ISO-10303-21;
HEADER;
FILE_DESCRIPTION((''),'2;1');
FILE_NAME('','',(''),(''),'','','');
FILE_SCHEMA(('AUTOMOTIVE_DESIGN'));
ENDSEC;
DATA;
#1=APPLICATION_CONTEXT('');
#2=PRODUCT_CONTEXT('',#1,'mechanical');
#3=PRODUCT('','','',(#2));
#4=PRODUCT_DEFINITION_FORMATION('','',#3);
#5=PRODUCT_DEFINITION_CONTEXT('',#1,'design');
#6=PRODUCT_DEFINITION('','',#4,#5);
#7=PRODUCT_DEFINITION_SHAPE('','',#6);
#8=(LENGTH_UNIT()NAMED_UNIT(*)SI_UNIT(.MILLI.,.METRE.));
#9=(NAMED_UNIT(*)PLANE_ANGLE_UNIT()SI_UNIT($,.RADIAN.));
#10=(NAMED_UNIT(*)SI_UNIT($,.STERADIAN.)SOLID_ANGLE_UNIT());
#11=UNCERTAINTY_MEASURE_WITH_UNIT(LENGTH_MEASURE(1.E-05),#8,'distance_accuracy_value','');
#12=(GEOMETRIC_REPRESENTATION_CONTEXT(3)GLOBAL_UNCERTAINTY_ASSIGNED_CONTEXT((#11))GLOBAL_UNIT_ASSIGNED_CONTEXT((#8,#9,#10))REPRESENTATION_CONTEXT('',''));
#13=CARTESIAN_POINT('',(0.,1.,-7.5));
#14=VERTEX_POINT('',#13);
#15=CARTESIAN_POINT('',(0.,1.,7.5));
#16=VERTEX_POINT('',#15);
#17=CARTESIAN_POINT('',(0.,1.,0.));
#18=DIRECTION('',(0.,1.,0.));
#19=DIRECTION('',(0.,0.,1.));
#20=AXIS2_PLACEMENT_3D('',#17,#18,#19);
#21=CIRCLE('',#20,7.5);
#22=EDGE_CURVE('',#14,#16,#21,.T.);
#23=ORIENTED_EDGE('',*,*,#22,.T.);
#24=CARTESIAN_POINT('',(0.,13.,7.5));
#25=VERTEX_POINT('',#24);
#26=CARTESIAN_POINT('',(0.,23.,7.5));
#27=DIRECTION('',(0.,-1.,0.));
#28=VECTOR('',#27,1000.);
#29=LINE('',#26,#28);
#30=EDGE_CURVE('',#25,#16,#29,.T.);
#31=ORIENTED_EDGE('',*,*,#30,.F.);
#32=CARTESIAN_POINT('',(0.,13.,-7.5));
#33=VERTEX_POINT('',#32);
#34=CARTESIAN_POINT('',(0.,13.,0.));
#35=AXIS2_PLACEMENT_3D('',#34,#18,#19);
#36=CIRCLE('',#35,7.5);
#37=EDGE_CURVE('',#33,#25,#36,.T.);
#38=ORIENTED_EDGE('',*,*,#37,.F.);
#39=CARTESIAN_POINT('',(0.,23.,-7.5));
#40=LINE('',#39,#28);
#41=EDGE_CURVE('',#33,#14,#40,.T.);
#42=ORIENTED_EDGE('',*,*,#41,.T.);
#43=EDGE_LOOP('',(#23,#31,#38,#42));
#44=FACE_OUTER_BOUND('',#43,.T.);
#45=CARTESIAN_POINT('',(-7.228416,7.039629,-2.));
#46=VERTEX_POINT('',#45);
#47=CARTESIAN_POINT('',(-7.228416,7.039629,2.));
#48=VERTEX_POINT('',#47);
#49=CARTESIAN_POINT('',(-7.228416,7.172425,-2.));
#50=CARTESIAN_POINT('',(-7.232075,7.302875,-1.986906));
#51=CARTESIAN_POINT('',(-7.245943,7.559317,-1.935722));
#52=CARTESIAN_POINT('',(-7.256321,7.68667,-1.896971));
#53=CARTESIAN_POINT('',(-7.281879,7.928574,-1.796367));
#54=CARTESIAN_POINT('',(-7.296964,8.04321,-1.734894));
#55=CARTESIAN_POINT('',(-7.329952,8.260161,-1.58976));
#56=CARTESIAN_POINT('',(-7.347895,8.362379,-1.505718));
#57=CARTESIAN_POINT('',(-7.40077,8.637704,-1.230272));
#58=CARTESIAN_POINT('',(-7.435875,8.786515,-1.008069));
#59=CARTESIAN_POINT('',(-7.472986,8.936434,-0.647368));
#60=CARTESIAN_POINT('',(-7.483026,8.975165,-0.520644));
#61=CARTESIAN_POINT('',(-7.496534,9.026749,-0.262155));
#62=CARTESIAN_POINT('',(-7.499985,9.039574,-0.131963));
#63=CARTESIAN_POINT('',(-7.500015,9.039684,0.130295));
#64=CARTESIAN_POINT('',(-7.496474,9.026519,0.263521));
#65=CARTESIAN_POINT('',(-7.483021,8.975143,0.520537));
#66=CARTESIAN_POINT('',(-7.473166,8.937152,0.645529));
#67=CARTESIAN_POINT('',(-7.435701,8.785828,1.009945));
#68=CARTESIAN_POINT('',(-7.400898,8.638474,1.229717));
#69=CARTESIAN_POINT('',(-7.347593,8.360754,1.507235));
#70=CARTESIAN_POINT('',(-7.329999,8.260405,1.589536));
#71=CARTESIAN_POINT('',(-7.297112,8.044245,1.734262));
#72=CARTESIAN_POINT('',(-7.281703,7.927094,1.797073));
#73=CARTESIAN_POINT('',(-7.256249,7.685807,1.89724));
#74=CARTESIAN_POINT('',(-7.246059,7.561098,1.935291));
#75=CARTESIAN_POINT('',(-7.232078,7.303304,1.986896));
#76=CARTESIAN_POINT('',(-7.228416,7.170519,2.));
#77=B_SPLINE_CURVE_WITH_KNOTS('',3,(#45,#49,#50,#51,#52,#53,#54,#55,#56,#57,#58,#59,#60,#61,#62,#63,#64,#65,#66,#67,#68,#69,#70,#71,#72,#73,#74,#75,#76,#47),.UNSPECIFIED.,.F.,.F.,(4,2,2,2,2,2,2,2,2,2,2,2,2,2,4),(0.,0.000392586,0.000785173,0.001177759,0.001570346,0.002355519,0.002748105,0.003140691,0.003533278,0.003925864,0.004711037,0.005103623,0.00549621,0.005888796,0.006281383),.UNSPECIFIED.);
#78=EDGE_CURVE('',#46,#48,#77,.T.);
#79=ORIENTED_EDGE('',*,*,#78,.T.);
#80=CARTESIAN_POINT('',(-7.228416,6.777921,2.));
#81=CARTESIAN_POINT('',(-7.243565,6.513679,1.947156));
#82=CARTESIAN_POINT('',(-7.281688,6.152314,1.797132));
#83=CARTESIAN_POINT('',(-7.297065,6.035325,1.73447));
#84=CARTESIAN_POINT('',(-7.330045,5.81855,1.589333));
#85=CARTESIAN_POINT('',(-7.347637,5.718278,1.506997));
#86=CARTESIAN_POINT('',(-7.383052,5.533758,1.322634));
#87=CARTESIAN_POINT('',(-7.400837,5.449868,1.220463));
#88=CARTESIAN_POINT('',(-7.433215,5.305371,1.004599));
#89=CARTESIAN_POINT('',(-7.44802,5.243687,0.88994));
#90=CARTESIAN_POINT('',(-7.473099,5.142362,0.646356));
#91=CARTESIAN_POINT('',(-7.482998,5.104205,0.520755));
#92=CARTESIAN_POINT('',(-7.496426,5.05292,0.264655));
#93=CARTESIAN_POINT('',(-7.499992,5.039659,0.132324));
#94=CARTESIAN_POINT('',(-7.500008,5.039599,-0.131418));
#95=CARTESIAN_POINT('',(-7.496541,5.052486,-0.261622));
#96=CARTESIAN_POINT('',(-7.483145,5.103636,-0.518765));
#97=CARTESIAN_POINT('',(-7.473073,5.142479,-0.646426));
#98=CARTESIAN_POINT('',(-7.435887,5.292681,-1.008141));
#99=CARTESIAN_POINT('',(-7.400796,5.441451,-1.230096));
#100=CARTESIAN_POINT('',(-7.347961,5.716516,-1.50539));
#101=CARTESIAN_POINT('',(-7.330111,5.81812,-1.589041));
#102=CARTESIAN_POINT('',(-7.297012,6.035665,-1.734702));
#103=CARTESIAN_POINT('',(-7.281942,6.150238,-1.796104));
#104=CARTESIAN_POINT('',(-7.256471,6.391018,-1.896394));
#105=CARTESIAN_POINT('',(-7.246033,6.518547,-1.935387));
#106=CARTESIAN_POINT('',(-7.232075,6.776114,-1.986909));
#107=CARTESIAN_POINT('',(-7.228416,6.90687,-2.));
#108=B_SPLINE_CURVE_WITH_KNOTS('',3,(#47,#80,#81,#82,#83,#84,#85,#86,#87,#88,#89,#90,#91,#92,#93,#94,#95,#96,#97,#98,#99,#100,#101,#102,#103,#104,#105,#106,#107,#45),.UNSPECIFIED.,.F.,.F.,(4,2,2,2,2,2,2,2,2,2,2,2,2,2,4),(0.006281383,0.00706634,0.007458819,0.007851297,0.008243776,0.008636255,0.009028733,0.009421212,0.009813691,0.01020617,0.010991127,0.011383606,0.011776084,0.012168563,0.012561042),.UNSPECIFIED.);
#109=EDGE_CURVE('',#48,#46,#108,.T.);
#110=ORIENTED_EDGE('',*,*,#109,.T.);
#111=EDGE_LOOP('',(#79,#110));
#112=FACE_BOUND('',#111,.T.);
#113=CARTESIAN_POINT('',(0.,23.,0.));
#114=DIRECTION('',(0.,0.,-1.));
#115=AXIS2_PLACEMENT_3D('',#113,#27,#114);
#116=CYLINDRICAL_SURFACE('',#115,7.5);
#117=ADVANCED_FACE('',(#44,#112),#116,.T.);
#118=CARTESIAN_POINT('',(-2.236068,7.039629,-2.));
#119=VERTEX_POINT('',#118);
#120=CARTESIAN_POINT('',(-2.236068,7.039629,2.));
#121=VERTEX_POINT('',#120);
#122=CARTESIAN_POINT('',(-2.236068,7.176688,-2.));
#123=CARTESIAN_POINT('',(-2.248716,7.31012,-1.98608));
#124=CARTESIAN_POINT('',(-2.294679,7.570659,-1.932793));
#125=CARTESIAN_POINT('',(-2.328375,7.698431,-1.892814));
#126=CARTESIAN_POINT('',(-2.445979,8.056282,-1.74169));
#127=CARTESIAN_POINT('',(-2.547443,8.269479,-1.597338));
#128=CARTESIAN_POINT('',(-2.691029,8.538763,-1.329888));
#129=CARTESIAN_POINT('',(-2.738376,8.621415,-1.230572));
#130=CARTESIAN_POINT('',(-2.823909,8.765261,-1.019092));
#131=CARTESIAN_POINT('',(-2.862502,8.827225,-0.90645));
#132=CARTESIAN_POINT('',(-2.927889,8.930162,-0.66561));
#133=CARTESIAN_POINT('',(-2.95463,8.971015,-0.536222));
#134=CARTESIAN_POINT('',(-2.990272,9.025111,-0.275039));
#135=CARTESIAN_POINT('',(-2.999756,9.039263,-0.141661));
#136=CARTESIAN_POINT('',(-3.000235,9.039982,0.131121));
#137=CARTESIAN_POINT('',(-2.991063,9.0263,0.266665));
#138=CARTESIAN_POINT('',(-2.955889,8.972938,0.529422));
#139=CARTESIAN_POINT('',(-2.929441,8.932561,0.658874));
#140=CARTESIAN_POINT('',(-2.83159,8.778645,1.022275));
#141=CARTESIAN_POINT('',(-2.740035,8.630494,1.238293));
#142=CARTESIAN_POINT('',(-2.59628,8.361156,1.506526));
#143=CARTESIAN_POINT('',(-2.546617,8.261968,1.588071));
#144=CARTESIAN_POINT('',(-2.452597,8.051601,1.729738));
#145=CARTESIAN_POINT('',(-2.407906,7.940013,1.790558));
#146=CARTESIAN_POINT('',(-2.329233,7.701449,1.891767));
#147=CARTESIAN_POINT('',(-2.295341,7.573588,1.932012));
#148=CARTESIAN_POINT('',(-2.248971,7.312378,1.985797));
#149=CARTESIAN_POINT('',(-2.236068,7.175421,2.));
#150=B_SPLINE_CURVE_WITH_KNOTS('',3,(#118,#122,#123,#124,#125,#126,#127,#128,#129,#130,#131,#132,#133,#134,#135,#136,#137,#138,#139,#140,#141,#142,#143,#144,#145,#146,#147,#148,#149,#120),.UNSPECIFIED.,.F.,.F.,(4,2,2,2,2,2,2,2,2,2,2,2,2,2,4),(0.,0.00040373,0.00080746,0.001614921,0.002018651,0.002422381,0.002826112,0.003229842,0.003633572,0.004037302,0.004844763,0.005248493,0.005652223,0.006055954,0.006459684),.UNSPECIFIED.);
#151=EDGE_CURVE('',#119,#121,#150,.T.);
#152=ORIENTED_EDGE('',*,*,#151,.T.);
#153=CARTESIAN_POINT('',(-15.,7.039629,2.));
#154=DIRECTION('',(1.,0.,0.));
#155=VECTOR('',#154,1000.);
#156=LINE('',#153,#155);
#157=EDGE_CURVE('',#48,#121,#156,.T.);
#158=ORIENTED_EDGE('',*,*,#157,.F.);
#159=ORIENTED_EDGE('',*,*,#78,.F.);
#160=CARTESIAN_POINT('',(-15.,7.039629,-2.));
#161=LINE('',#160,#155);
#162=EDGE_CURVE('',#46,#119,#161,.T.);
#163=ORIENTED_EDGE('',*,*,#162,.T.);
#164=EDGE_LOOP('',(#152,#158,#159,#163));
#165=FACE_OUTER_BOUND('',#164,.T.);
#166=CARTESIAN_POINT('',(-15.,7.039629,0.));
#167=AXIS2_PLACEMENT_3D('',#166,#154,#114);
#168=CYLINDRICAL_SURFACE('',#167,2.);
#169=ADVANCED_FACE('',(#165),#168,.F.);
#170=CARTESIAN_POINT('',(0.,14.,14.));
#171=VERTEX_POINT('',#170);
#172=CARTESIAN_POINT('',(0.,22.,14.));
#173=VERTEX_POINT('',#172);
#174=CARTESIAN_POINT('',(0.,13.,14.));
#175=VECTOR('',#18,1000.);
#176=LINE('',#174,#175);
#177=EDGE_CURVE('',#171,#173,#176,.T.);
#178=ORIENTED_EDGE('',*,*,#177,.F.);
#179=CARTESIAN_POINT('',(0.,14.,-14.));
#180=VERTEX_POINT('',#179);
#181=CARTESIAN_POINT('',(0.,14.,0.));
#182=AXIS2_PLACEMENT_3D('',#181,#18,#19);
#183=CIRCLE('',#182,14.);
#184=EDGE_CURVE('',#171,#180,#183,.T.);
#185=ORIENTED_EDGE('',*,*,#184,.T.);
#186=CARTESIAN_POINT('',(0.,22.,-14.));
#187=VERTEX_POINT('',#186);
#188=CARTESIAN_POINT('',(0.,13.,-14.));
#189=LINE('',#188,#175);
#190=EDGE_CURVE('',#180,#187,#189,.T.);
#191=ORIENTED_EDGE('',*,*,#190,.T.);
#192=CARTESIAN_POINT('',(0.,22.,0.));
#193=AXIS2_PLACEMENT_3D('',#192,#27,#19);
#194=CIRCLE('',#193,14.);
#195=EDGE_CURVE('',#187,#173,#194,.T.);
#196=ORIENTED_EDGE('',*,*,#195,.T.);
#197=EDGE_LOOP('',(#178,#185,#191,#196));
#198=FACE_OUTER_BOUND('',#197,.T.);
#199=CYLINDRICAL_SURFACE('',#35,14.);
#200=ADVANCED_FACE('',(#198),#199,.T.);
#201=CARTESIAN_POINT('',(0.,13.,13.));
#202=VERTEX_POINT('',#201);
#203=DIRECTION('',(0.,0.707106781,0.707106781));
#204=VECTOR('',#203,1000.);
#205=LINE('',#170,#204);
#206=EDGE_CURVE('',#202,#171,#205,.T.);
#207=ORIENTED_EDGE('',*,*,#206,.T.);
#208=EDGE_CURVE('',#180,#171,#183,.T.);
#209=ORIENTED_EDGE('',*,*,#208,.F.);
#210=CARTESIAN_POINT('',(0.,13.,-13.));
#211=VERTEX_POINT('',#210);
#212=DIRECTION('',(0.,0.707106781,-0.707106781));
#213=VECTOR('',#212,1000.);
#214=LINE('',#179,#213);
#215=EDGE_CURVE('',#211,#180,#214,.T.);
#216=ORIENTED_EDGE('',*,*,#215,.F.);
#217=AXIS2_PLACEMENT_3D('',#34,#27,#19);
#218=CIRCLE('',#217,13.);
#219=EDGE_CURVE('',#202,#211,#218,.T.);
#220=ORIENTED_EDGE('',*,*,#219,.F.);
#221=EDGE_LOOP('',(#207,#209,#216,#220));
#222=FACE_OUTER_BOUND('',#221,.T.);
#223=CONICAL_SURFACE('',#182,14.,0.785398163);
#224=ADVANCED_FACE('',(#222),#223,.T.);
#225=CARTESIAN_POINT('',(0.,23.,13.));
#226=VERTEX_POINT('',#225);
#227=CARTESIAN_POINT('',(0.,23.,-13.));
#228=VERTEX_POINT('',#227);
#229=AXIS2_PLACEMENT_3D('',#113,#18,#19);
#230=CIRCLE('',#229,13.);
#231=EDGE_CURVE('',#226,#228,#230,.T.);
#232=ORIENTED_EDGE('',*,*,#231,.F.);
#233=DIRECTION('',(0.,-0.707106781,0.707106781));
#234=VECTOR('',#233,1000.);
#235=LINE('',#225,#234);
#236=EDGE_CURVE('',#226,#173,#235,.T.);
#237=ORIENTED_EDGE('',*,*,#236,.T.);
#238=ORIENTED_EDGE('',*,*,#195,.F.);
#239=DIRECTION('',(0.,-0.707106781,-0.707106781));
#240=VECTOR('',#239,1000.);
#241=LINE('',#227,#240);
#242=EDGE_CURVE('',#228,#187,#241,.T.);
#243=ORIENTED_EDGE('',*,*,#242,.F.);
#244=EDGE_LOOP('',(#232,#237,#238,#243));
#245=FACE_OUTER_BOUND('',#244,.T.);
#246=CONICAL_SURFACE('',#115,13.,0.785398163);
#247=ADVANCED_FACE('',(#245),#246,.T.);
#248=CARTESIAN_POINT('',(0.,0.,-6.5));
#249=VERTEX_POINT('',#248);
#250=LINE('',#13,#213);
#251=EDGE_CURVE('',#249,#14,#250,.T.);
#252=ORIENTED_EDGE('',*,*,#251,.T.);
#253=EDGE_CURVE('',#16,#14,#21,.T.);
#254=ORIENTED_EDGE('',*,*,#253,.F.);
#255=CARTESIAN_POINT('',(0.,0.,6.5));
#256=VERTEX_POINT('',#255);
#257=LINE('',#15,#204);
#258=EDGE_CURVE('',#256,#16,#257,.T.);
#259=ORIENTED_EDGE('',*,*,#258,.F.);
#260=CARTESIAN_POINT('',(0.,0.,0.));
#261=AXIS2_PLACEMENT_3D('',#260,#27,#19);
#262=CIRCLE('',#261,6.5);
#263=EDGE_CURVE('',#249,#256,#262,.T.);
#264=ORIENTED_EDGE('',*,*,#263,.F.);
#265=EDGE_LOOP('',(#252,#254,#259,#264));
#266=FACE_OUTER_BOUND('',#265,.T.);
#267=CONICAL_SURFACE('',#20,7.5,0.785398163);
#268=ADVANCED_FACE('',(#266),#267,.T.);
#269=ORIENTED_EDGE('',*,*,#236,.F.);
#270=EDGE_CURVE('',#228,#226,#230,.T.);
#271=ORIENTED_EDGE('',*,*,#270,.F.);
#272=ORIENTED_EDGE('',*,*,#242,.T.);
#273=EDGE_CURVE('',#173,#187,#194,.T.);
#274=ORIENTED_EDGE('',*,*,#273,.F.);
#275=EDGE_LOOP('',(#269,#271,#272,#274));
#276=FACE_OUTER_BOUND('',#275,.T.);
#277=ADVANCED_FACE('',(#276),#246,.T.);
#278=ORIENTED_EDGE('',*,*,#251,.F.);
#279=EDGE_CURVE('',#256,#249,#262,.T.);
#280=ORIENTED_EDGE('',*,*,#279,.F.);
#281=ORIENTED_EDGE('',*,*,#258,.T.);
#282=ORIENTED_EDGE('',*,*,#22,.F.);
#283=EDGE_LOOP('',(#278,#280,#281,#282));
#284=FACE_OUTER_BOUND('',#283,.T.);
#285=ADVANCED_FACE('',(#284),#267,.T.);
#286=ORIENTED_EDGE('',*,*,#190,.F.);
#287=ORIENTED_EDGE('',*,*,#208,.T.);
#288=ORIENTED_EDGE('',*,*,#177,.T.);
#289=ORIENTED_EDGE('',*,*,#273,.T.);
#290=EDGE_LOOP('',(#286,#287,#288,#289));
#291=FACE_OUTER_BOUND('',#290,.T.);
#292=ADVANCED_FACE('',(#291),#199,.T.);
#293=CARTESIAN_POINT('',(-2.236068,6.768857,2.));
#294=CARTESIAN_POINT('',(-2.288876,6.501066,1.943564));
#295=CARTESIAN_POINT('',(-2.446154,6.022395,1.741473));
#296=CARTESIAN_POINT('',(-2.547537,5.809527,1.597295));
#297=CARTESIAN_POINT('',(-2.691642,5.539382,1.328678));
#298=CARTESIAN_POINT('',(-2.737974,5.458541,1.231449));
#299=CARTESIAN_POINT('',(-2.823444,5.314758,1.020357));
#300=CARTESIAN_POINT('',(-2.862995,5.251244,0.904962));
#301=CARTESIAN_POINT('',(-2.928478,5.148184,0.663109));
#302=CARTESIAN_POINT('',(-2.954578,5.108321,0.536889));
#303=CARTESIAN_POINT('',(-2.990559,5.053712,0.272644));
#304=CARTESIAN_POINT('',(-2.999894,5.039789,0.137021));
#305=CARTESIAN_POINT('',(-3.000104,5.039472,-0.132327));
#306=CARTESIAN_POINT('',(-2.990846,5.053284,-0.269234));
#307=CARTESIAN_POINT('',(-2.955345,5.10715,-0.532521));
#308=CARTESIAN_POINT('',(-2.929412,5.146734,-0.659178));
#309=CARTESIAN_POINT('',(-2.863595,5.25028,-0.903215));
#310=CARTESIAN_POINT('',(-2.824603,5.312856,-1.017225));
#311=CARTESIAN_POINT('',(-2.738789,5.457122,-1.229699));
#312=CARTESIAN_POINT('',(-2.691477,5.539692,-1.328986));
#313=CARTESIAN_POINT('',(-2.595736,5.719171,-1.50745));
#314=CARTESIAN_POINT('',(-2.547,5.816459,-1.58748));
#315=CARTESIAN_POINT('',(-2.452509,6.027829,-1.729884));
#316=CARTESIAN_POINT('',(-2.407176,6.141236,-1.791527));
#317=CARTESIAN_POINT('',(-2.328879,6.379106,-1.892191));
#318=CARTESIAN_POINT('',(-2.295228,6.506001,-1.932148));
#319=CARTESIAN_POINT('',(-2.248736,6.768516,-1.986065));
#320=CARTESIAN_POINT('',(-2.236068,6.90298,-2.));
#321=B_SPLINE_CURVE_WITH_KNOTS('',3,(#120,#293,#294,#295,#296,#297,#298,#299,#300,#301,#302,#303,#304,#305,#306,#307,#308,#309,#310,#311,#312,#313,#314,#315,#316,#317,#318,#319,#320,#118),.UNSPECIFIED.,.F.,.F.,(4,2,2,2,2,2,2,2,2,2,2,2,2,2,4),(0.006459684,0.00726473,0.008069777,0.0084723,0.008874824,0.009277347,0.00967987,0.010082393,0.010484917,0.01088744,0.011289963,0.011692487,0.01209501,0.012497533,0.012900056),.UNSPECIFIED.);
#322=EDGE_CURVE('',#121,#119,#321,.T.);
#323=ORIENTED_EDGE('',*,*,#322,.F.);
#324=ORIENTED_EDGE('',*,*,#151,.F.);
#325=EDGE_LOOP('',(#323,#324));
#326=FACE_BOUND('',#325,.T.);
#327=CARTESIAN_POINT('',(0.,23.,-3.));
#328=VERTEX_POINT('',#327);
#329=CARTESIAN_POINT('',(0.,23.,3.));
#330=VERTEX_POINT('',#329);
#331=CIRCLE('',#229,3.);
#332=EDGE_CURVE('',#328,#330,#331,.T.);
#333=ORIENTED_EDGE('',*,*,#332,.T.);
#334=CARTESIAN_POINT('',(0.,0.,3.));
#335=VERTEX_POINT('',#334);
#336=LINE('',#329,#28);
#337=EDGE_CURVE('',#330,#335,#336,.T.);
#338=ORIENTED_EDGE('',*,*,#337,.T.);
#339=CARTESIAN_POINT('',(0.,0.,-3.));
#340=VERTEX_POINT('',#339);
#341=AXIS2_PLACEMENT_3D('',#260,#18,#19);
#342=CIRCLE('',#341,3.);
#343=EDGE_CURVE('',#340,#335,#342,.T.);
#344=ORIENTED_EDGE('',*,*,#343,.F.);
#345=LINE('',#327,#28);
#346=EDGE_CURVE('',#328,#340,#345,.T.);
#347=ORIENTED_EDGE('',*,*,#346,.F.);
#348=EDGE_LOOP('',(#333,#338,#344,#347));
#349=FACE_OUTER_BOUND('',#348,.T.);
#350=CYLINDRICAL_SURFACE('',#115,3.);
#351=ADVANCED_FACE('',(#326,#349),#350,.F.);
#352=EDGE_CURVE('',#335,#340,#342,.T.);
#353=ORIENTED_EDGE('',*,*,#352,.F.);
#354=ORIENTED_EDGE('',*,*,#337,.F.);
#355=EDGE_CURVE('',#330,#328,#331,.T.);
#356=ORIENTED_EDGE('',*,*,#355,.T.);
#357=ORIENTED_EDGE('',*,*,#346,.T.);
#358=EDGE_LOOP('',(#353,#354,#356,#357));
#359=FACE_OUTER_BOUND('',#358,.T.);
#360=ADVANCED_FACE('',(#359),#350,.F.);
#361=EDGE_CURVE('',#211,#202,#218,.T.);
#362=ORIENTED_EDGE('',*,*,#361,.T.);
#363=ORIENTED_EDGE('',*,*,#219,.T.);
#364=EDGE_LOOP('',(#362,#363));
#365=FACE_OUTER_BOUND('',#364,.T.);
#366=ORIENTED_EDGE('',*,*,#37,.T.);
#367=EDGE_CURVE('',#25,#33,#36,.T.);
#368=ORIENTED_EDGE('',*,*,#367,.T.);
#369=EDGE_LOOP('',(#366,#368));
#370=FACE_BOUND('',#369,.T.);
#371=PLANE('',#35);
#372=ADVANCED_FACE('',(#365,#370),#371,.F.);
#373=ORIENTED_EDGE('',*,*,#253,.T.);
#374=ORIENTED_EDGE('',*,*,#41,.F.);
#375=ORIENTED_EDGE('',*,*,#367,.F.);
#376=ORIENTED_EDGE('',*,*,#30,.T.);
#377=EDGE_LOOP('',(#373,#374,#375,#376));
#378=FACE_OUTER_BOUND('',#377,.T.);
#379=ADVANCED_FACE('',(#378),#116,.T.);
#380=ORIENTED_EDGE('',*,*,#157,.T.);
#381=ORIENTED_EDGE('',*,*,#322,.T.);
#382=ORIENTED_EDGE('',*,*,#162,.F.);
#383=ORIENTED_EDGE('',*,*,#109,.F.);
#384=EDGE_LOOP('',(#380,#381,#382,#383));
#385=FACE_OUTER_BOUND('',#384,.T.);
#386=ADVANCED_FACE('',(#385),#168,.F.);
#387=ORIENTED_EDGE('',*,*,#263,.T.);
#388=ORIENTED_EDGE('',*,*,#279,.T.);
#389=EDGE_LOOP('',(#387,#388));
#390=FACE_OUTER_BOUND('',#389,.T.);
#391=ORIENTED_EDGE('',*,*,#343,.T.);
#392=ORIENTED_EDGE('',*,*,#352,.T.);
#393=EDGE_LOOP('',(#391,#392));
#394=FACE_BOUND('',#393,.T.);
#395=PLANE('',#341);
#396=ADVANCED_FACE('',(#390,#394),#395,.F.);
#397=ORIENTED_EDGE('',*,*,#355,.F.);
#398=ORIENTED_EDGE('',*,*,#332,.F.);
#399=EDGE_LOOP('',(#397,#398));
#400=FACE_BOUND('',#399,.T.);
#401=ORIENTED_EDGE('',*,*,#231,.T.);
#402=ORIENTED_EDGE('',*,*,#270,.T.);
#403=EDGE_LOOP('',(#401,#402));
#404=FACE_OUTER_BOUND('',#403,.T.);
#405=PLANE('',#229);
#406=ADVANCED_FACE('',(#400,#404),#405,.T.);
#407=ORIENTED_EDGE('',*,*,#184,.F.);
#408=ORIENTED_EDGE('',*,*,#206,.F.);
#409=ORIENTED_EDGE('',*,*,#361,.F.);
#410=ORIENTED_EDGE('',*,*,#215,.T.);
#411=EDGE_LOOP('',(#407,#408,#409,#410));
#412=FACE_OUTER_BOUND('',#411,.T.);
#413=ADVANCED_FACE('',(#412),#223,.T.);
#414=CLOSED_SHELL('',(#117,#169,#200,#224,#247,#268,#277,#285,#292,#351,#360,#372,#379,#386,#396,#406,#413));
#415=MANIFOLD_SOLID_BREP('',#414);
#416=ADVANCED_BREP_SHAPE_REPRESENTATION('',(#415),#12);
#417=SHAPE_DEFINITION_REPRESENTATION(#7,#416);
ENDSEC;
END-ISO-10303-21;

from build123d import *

# Parameters (mm, degrees)
SKETCH1_R           = 7.5
SKETCH1_R_2         = 3
BOSS_EXTRUDE1_DEPTH = 23
BOSS_EXTRUDE2_START = -10
SKETCH2_R           = 14
SKETCH2_R_2         = 3
BOSS_EXTRUDE2_DEPTH = 10
CHAMFER1_SIZE       = 1
SKETCH3_R           = 2
CUT_EXTRUDE1_DEPTH  = 15


with BuildPart() as part:
    # Sketch1 → Boss-Extrude1 (new body)
    with BuildSketch(Plane(origin=(0, 0, 0), x_dir=(1, 0, 0), z_dir=(0, 1, 0))):
        with Locations(Location((0, 0, 0), (0, 0, 270))):
            Circle(SKETCH1_R)
        with Locations(Location((0, 0, 0), (0, 0, 270))):
            Circle(SKETCH1_R_2, mode=Mode.SUBTRACT)
    extrude(amount=BOSS_EXTRUDE1_DEPTH)

    # Sketch2 → Boss-Extrude2 (add)
    with BuildSketch(Plane(origin=(0, 23, 0), x_dir=(1, 0, 0), z_dir=(0, 1, 0)).offset(BOSS_EXTRUDE2_START)):
        with Locations(Location((0, 0, 0), (0, 0, 270))):
            Circle(SKETCH2_R)
        with Locations(Location((0, 0, 0), (0, 0, 270))):
            Circle(SKETCH2_R_2, mode=Mode.SUBTRACT)
    extrude(amount=BOSS_EXTRUDE2_DEPTH)

    # Chamfer1
    chamfer1_edges = [part.edges().sort_by_distance(p)[0] for p in [
        (0, 23, -14),
        (0, 13, -14),
        (0, 0, -7.5),
    ]]
    chamfer(chamfer1_edges, length=CHAMFER1_SIZE)

    # Sketch3 → Cut-Extrude1 (cut)
    with BuildSketch(Plane(origin=(0, 0, 0), x_dir=(0, 0, -1), z_dir=(1, 0, 0))):
        with Locations((0, 7.039629159)):
            Circle(SKETCH3_R)
    extrude(amount=-CUT_EXTRUDE1_DEPTH, mode=Mode.SUBTRACT)


solid = part.part
